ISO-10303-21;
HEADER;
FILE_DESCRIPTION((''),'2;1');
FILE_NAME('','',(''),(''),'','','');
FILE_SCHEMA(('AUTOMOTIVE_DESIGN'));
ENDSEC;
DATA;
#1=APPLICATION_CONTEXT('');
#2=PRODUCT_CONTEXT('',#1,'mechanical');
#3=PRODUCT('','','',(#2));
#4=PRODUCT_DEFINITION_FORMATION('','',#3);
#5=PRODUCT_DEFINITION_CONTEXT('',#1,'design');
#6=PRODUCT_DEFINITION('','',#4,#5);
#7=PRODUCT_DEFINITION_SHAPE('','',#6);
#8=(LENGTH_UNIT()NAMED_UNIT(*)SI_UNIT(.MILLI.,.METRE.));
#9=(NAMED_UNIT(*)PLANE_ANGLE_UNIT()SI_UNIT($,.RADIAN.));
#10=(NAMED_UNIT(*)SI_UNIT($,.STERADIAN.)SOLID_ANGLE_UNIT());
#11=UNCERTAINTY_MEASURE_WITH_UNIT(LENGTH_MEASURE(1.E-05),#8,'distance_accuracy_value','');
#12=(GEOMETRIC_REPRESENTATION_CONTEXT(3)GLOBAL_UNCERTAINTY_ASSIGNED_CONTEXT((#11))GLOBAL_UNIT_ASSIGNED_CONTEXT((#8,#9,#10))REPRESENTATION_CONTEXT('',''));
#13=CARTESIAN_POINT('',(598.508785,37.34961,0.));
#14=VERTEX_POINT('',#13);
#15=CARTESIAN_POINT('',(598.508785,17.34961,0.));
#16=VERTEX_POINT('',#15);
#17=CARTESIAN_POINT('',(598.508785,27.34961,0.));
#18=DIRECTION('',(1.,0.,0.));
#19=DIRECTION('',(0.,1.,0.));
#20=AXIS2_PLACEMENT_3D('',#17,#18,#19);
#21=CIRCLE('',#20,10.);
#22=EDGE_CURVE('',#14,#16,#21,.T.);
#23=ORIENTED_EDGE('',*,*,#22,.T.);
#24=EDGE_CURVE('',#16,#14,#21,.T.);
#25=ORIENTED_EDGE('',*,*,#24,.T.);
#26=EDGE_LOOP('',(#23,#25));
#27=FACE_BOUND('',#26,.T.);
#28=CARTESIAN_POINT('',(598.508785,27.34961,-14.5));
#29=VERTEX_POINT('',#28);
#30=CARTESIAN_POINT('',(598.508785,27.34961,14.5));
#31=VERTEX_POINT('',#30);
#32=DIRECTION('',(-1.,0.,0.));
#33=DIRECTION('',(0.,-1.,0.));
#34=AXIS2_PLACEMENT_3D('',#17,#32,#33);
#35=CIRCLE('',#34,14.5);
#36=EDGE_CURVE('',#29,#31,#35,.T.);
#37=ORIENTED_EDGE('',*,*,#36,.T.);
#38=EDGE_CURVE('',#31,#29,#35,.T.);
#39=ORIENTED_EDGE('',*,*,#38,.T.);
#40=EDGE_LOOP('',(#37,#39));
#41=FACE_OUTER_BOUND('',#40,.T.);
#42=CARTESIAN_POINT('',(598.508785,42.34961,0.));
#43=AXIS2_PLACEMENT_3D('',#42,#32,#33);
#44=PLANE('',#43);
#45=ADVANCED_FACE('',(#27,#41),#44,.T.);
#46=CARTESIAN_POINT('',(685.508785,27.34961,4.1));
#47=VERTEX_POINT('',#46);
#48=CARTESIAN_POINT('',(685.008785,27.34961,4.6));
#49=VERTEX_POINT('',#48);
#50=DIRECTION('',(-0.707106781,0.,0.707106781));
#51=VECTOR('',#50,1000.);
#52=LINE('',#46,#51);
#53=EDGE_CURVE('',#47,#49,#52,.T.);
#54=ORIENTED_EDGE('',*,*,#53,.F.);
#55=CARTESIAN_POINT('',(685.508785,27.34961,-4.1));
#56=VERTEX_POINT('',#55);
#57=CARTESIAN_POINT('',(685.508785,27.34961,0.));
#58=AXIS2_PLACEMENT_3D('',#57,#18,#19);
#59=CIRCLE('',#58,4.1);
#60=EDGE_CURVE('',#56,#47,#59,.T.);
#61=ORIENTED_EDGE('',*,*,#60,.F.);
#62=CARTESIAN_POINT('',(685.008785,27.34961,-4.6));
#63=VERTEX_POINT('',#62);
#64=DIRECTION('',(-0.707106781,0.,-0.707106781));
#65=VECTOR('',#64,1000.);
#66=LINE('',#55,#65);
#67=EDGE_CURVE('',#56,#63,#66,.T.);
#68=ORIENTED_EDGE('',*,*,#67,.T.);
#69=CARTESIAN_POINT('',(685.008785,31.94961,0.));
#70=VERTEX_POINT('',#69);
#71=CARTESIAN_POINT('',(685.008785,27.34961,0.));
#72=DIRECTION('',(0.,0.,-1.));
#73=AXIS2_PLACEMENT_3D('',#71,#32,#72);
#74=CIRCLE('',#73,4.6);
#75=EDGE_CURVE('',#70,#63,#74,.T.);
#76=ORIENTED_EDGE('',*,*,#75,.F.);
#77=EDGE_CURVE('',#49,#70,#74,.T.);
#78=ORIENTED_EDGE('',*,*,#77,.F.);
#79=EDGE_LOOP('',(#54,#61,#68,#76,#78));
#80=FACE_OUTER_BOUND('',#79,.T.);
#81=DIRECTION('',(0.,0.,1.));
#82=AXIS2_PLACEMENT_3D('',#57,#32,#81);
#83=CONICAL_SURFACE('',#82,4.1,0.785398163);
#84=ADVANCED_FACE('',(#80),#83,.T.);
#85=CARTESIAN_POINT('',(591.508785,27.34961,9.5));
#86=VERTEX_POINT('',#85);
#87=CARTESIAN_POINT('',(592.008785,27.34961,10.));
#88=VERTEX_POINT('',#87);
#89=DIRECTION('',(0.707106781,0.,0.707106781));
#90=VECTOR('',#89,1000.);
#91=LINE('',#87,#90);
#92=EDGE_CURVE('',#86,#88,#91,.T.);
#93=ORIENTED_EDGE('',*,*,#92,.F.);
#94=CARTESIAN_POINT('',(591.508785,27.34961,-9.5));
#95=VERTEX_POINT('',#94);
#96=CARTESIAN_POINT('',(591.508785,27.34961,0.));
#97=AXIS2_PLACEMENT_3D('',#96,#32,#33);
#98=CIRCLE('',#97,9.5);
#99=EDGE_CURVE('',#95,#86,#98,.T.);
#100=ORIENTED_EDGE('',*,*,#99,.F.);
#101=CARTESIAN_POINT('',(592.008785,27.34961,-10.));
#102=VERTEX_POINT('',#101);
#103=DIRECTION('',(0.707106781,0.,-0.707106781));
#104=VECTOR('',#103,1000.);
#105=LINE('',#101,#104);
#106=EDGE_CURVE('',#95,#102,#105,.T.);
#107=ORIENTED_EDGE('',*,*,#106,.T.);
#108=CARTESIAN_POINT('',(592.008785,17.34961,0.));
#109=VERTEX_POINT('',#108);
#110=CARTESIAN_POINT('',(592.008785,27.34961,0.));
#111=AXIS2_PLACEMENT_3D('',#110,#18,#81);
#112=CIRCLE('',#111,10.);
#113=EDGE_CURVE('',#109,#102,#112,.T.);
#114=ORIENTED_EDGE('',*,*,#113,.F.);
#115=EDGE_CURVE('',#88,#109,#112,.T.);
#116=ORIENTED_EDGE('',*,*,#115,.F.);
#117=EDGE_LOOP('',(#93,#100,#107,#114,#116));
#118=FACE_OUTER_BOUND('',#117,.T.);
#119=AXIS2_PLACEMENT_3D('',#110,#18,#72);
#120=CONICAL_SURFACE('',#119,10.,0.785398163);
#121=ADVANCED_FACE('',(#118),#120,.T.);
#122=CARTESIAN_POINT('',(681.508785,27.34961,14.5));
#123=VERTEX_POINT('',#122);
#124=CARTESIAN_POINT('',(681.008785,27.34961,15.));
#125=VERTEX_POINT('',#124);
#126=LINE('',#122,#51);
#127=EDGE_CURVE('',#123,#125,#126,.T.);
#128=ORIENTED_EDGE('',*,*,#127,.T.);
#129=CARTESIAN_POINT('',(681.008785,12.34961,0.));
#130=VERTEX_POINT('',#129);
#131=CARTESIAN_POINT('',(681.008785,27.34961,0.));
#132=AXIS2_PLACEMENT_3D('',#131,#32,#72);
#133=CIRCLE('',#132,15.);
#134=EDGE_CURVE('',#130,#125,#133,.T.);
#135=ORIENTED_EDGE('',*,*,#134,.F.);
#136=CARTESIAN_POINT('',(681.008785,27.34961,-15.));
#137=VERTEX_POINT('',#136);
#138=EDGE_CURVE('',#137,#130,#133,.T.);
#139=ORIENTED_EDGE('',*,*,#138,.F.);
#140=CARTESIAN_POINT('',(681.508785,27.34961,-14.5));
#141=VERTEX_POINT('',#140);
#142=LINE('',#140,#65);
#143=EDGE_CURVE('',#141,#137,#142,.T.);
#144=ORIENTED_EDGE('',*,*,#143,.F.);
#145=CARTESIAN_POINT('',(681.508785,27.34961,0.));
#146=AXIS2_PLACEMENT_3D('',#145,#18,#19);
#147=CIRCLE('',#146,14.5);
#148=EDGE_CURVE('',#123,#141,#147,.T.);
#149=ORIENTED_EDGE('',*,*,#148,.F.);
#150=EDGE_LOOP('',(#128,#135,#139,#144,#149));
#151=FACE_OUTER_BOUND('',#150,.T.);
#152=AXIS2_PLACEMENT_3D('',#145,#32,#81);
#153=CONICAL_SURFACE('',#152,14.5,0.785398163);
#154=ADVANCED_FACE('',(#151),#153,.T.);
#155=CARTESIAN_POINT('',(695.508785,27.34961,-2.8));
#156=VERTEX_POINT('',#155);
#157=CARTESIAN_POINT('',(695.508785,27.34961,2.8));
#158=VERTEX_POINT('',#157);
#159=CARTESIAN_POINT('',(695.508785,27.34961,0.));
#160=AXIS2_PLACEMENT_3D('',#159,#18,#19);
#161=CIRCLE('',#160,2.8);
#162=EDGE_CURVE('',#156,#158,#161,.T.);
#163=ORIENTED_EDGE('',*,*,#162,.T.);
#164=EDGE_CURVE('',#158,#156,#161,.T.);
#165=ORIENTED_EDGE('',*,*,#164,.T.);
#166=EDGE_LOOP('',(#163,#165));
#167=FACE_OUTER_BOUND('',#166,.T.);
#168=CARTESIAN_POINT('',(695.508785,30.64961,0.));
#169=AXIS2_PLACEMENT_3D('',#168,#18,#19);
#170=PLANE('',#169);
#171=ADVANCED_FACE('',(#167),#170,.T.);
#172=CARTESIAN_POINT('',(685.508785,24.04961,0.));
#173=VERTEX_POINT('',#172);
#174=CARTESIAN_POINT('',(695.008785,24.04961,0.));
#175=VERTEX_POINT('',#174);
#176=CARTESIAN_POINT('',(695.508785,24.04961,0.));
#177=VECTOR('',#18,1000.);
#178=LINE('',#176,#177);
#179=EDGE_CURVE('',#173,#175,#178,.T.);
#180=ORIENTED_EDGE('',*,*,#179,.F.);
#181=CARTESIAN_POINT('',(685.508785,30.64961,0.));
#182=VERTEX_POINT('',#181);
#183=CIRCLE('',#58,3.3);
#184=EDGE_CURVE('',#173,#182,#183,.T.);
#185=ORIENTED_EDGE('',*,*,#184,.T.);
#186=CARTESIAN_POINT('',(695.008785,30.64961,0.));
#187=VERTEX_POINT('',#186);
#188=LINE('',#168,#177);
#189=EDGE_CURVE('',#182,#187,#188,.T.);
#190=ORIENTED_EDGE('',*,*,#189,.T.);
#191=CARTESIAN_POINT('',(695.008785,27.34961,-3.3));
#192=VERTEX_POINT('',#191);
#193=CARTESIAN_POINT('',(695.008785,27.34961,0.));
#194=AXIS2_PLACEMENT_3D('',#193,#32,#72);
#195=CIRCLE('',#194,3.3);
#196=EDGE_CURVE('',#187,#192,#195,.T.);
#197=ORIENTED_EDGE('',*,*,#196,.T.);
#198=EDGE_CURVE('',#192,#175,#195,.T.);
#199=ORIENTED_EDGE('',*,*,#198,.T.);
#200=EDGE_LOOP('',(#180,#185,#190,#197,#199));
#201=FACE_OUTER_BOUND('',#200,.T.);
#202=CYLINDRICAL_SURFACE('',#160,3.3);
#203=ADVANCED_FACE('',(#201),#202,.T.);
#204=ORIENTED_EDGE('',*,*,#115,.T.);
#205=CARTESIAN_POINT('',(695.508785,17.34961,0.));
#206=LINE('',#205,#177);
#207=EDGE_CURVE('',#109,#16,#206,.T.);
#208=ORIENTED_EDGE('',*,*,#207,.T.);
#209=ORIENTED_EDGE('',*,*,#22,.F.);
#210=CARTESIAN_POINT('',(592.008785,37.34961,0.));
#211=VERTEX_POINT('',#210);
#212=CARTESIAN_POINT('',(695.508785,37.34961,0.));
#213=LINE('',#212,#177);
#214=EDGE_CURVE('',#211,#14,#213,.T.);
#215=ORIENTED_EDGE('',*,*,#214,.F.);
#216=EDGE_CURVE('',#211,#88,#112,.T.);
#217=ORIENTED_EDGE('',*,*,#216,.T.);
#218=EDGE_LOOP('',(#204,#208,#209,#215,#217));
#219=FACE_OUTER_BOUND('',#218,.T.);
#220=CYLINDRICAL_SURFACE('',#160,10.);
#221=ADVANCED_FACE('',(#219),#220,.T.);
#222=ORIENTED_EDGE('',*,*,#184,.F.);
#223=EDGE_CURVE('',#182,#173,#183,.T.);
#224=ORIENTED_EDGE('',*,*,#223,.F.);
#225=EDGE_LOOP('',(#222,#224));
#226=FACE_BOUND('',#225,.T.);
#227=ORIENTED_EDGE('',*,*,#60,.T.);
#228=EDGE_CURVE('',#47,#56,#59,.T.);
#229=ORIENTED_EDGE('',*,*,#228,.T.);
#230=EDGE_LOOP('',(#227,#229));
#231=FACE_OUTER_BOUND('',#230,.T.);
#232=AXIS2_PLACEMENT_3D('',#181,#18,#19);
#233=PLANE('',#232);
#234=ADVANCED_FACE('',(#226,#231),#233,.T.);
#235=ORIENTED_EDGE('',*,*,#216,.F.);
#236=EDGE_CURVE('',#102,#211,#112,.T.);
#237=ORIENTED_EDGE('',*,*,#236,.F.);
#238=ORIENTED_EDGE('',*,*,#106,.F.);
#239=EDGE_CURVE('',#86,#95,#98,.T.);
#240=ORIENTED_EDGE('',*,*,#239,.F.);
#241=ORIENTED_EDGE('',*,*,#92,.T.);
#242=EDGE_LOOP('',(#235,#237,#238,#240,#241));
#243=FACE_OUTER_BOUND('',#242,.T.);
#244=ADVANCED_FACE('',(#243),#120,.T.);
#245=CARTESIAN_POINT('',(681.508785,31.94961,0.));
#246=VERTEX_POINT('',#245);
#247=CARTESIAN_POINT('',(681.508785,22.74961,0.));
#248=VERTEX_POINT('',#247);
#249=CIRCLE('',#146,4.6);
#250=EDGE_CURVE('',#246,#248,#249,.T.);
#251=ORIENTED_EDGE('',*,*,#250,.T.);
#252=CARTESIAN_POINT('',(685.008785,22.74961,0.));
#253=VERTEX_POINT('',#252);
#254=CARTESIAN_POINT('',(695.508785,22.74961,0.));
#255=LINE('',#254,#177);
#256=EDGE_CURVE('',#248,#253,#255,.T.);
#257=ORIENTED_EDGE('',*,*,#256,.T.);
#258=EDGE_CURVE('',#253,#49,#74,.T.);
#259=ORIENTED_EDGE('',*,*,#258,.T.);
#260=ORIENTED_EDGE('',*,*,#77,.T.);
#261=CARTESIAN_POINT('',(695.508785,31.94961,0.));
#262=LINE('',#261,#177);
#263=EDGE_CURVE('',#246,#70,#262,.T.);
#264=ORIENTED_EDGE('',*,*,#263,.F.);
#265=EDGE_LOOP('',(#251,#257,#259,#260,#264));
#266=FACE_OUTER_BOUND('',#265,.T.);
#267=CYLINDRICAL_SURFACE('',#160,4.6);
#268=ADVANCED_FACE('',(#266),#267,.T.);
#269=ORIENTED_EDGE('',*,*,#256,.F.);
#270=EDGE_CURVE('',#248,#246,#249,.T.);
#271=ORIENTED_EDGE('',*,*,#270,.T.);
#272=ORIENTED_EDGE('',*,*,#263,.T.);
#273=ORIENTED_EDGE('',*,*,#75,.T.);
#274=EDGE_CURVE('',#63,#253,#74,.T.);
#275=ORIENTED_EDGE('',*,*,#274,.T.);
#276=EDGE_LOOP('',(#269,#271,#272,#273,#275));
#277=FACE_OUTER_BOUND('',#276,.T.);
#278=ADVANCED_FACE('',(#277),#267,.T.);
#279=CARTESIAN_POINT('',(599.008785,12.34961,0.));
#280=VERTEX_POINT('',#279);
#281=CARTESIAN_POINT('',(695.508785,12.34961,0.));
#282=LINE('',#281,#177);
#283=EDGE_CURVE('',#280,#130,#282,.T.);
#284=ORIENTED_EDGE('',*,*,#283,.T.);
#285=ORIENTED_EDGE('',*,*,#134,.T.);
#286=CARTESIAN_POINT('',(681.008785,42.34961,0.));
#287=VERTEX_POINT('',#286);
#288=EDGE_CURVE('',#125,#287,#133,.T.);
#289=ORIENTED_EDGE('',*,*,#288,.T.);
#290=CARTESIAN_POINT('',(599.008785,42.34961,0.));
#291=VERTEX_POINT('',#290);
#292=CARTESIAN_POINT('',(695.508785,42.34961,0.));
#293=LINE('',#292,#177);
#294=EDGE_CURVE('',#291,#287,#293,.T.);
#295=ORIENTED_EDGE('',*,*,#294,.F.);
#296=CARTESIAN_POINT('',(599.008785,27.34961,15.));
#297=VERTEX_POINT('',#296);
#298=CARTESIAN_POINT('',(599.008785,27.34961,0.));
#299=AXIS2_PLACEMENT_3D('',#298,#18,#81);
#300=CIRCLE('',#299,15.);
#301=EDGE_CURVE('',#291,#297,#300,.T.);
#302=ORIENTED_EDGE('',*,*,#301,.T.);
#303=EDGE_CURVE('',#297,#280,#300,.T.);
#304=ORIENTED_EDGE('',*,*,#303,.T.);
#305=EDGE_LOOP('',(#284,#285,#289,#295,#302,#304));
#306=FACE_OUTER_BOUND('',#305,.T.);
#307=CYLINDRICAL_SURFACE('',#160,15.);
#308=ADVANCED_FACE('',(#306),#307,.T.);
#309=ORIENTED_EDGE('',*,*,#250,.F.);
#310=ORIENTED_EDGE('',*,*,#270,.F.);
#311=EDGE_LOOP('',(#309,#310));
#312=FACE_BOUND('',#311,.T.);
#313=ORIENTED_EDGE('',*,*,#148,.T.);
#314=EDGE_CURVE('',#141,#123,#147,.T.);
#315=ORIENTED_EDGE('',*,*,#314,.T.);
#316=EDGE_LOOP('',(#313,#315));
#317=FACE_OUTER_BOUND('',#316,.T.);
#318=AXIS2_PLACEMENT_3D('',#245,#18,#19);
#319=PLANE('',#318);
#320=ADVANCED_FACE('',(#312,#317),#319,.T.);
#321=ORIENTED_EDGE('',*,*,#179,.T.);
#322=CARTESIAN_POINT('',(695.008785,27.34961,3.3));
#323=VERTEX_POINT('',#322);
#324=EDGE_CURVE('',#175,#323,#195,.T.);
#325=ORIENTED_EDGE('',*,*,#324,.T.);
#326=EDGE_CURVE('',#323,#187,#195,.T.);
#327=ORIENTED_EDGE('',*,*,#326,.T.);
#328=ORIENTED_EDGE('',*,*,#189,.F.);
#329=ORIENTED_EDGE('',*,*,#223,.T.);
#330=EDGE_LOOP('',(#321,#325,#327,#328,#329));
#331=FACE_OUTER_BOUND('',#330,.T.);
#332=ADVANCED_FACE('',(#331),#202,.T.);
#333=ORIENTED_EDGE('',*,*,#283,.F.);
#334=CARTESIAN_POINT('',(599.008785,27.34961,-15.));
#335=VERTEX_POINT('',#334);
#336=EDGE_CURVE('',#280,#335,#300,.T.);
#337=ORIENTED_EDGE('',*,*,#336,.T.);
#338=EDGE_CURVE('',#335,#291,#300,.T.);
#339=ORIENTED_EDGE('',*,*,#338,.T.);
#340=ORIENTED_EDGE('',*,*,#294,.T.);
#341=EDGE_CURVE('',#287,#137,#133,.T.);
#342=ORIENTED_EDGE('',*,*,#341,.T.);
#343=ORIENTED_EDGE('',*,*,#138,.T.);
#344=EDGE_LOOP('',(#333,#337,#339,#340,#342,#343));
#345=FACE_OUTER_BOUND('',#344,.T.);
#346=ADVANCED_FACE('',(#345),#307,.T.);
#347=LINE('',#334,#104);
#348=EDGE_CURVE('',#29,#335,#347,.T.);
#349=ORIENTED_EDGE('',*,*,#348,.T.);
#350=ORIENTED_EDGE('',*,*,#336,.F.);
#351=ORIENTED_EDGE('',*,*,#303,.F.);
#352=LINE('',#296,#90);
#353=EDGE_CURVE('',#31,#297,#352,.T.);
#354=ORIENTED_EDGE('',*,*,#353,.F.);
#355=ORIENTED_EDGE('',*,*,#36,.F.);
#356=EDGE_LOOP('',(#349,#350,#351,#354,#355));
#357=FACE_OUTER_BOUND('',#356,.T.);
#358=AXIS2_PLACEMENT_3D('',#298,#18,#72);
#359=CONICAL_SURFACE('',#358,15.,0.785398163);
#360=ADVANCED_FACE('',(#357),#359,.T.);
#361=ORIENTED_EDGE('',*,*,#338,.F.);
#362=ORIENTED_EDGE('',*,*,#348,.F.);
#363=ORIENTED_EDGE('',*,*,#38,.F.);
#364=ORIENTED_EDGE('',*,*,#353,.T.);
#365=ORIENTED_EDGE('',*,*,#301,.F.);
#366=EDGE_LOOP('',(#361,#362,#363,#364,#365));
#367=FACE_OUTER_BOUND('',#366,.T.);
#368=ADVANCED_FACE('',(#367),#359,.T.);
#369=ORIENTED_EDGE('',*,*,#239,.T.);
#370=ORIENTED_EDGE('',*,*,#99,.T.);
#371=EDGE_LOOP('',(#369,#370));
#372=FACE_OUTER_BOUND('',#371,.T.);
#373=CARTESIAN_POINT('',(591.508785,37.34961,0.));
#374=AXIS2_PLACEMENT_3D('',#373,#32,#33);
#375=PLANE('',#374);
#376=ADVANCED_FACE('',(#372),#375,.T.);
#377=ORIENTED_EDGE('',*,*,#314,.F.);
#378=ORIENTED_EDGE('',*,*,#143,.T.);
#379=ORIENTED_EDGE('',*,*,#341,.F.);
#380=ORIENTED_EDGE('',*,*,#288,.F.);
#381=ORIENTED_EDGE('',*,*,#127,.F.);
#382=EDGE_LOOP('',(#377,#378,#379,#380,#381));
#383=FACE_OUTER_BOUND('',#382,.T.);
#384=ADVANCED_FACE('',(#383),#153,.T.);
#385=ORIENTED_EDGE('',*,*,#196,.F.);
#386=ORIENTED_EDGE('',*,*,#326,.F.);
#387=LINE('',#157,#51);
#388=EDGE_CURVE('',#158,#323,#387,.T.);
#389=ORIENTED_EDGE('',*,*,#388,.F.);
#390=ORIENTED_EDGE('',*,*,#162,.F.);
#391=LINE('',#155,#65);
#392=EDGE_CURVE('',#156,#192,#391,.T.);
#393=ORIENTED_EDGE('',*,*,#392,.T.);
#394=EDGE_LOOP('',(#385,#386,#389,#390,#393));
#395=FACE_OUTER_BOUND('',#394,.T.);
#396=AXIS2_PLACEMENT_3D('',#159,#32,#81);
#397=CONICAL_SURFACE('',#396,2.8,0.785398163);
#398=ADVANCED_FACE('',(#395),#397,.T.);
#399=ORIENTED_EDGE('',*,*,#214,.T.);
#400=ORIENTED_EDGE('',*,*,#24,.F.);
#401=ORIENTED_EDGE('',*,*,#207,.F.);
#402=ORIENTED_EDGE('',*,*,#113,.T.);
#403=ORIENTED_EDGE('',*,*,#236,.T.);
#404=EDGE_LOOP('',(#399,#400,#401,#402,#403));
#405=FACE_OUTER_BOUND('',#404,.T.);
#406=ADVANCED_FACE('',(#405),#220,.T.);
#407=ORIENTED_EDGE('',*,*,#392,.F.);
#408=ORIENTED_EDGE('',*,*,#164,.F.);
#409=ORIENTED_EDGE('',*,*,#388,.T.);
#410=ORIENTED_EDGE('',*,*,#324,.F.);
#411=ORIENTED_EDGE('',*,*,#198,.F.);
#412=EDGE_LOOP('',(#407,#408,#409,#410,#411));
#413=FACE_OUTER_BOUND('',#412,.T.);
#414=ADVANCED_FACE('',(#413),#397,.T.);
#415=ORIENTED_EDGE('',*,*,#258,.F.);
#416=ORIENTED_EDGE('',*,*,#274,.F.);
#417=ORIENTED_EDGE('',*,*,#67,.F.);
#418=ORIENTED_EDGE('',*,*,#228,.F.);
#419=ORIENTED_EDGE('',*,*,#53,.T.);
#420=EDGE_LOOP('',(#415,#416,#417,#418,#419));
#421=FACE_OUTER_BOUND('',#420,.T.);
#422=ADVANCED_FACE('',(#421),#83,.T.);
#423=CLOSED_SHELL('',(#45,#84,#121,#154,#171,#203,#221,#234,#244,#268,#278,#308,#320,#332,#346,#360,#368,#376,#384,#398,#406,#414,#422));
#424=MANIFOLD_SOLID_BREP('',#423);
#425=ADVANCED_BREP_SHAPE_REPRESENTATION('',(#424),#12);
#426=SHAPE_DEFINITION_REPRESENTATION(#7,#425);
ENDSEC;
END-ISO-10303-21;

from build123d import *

# Parameters (mm, degrees)
CHAMFER1_SIZE = 0.5


with BuildPart() as part:
    # Sketch1 → Revolve1 (revolve)
    with BuildSketch(Plane.XY):
        Polygon((695.508784709, 30.649610335), (685.508784709, 30.649610335), (685.508784709, 31.949610335), (681.508784709, 31.949610335), (681.508784709, 42.349610335), (598.508784709, 42.349610335), (598.508784709, 37.349610335), (591.508784709, 37.349610335), (591.508784709, 27.349610335), (695.508784709, 27.349610335), align=None)
    revolve(axis=Axis((695.508784709, 27.349610335, 0), (-1, 0, 0)))

    # Chamfer1
    chamfer1_edges = [part.edges().sort_by_distance(p)[0] for p in [
        (695.508784709, 24.049610335, 0),
        (685.508784709, 22.749610335, 0),
        (681.508784709, 12.349610335, 0),
        (598.508784709, 12.349610335, 0),
        (591.508784709, 17.349610335, 0),
    ]]
    chamfer(chamfer1_edges, length=CHAMFER1_SIZE)


solid = part.part
